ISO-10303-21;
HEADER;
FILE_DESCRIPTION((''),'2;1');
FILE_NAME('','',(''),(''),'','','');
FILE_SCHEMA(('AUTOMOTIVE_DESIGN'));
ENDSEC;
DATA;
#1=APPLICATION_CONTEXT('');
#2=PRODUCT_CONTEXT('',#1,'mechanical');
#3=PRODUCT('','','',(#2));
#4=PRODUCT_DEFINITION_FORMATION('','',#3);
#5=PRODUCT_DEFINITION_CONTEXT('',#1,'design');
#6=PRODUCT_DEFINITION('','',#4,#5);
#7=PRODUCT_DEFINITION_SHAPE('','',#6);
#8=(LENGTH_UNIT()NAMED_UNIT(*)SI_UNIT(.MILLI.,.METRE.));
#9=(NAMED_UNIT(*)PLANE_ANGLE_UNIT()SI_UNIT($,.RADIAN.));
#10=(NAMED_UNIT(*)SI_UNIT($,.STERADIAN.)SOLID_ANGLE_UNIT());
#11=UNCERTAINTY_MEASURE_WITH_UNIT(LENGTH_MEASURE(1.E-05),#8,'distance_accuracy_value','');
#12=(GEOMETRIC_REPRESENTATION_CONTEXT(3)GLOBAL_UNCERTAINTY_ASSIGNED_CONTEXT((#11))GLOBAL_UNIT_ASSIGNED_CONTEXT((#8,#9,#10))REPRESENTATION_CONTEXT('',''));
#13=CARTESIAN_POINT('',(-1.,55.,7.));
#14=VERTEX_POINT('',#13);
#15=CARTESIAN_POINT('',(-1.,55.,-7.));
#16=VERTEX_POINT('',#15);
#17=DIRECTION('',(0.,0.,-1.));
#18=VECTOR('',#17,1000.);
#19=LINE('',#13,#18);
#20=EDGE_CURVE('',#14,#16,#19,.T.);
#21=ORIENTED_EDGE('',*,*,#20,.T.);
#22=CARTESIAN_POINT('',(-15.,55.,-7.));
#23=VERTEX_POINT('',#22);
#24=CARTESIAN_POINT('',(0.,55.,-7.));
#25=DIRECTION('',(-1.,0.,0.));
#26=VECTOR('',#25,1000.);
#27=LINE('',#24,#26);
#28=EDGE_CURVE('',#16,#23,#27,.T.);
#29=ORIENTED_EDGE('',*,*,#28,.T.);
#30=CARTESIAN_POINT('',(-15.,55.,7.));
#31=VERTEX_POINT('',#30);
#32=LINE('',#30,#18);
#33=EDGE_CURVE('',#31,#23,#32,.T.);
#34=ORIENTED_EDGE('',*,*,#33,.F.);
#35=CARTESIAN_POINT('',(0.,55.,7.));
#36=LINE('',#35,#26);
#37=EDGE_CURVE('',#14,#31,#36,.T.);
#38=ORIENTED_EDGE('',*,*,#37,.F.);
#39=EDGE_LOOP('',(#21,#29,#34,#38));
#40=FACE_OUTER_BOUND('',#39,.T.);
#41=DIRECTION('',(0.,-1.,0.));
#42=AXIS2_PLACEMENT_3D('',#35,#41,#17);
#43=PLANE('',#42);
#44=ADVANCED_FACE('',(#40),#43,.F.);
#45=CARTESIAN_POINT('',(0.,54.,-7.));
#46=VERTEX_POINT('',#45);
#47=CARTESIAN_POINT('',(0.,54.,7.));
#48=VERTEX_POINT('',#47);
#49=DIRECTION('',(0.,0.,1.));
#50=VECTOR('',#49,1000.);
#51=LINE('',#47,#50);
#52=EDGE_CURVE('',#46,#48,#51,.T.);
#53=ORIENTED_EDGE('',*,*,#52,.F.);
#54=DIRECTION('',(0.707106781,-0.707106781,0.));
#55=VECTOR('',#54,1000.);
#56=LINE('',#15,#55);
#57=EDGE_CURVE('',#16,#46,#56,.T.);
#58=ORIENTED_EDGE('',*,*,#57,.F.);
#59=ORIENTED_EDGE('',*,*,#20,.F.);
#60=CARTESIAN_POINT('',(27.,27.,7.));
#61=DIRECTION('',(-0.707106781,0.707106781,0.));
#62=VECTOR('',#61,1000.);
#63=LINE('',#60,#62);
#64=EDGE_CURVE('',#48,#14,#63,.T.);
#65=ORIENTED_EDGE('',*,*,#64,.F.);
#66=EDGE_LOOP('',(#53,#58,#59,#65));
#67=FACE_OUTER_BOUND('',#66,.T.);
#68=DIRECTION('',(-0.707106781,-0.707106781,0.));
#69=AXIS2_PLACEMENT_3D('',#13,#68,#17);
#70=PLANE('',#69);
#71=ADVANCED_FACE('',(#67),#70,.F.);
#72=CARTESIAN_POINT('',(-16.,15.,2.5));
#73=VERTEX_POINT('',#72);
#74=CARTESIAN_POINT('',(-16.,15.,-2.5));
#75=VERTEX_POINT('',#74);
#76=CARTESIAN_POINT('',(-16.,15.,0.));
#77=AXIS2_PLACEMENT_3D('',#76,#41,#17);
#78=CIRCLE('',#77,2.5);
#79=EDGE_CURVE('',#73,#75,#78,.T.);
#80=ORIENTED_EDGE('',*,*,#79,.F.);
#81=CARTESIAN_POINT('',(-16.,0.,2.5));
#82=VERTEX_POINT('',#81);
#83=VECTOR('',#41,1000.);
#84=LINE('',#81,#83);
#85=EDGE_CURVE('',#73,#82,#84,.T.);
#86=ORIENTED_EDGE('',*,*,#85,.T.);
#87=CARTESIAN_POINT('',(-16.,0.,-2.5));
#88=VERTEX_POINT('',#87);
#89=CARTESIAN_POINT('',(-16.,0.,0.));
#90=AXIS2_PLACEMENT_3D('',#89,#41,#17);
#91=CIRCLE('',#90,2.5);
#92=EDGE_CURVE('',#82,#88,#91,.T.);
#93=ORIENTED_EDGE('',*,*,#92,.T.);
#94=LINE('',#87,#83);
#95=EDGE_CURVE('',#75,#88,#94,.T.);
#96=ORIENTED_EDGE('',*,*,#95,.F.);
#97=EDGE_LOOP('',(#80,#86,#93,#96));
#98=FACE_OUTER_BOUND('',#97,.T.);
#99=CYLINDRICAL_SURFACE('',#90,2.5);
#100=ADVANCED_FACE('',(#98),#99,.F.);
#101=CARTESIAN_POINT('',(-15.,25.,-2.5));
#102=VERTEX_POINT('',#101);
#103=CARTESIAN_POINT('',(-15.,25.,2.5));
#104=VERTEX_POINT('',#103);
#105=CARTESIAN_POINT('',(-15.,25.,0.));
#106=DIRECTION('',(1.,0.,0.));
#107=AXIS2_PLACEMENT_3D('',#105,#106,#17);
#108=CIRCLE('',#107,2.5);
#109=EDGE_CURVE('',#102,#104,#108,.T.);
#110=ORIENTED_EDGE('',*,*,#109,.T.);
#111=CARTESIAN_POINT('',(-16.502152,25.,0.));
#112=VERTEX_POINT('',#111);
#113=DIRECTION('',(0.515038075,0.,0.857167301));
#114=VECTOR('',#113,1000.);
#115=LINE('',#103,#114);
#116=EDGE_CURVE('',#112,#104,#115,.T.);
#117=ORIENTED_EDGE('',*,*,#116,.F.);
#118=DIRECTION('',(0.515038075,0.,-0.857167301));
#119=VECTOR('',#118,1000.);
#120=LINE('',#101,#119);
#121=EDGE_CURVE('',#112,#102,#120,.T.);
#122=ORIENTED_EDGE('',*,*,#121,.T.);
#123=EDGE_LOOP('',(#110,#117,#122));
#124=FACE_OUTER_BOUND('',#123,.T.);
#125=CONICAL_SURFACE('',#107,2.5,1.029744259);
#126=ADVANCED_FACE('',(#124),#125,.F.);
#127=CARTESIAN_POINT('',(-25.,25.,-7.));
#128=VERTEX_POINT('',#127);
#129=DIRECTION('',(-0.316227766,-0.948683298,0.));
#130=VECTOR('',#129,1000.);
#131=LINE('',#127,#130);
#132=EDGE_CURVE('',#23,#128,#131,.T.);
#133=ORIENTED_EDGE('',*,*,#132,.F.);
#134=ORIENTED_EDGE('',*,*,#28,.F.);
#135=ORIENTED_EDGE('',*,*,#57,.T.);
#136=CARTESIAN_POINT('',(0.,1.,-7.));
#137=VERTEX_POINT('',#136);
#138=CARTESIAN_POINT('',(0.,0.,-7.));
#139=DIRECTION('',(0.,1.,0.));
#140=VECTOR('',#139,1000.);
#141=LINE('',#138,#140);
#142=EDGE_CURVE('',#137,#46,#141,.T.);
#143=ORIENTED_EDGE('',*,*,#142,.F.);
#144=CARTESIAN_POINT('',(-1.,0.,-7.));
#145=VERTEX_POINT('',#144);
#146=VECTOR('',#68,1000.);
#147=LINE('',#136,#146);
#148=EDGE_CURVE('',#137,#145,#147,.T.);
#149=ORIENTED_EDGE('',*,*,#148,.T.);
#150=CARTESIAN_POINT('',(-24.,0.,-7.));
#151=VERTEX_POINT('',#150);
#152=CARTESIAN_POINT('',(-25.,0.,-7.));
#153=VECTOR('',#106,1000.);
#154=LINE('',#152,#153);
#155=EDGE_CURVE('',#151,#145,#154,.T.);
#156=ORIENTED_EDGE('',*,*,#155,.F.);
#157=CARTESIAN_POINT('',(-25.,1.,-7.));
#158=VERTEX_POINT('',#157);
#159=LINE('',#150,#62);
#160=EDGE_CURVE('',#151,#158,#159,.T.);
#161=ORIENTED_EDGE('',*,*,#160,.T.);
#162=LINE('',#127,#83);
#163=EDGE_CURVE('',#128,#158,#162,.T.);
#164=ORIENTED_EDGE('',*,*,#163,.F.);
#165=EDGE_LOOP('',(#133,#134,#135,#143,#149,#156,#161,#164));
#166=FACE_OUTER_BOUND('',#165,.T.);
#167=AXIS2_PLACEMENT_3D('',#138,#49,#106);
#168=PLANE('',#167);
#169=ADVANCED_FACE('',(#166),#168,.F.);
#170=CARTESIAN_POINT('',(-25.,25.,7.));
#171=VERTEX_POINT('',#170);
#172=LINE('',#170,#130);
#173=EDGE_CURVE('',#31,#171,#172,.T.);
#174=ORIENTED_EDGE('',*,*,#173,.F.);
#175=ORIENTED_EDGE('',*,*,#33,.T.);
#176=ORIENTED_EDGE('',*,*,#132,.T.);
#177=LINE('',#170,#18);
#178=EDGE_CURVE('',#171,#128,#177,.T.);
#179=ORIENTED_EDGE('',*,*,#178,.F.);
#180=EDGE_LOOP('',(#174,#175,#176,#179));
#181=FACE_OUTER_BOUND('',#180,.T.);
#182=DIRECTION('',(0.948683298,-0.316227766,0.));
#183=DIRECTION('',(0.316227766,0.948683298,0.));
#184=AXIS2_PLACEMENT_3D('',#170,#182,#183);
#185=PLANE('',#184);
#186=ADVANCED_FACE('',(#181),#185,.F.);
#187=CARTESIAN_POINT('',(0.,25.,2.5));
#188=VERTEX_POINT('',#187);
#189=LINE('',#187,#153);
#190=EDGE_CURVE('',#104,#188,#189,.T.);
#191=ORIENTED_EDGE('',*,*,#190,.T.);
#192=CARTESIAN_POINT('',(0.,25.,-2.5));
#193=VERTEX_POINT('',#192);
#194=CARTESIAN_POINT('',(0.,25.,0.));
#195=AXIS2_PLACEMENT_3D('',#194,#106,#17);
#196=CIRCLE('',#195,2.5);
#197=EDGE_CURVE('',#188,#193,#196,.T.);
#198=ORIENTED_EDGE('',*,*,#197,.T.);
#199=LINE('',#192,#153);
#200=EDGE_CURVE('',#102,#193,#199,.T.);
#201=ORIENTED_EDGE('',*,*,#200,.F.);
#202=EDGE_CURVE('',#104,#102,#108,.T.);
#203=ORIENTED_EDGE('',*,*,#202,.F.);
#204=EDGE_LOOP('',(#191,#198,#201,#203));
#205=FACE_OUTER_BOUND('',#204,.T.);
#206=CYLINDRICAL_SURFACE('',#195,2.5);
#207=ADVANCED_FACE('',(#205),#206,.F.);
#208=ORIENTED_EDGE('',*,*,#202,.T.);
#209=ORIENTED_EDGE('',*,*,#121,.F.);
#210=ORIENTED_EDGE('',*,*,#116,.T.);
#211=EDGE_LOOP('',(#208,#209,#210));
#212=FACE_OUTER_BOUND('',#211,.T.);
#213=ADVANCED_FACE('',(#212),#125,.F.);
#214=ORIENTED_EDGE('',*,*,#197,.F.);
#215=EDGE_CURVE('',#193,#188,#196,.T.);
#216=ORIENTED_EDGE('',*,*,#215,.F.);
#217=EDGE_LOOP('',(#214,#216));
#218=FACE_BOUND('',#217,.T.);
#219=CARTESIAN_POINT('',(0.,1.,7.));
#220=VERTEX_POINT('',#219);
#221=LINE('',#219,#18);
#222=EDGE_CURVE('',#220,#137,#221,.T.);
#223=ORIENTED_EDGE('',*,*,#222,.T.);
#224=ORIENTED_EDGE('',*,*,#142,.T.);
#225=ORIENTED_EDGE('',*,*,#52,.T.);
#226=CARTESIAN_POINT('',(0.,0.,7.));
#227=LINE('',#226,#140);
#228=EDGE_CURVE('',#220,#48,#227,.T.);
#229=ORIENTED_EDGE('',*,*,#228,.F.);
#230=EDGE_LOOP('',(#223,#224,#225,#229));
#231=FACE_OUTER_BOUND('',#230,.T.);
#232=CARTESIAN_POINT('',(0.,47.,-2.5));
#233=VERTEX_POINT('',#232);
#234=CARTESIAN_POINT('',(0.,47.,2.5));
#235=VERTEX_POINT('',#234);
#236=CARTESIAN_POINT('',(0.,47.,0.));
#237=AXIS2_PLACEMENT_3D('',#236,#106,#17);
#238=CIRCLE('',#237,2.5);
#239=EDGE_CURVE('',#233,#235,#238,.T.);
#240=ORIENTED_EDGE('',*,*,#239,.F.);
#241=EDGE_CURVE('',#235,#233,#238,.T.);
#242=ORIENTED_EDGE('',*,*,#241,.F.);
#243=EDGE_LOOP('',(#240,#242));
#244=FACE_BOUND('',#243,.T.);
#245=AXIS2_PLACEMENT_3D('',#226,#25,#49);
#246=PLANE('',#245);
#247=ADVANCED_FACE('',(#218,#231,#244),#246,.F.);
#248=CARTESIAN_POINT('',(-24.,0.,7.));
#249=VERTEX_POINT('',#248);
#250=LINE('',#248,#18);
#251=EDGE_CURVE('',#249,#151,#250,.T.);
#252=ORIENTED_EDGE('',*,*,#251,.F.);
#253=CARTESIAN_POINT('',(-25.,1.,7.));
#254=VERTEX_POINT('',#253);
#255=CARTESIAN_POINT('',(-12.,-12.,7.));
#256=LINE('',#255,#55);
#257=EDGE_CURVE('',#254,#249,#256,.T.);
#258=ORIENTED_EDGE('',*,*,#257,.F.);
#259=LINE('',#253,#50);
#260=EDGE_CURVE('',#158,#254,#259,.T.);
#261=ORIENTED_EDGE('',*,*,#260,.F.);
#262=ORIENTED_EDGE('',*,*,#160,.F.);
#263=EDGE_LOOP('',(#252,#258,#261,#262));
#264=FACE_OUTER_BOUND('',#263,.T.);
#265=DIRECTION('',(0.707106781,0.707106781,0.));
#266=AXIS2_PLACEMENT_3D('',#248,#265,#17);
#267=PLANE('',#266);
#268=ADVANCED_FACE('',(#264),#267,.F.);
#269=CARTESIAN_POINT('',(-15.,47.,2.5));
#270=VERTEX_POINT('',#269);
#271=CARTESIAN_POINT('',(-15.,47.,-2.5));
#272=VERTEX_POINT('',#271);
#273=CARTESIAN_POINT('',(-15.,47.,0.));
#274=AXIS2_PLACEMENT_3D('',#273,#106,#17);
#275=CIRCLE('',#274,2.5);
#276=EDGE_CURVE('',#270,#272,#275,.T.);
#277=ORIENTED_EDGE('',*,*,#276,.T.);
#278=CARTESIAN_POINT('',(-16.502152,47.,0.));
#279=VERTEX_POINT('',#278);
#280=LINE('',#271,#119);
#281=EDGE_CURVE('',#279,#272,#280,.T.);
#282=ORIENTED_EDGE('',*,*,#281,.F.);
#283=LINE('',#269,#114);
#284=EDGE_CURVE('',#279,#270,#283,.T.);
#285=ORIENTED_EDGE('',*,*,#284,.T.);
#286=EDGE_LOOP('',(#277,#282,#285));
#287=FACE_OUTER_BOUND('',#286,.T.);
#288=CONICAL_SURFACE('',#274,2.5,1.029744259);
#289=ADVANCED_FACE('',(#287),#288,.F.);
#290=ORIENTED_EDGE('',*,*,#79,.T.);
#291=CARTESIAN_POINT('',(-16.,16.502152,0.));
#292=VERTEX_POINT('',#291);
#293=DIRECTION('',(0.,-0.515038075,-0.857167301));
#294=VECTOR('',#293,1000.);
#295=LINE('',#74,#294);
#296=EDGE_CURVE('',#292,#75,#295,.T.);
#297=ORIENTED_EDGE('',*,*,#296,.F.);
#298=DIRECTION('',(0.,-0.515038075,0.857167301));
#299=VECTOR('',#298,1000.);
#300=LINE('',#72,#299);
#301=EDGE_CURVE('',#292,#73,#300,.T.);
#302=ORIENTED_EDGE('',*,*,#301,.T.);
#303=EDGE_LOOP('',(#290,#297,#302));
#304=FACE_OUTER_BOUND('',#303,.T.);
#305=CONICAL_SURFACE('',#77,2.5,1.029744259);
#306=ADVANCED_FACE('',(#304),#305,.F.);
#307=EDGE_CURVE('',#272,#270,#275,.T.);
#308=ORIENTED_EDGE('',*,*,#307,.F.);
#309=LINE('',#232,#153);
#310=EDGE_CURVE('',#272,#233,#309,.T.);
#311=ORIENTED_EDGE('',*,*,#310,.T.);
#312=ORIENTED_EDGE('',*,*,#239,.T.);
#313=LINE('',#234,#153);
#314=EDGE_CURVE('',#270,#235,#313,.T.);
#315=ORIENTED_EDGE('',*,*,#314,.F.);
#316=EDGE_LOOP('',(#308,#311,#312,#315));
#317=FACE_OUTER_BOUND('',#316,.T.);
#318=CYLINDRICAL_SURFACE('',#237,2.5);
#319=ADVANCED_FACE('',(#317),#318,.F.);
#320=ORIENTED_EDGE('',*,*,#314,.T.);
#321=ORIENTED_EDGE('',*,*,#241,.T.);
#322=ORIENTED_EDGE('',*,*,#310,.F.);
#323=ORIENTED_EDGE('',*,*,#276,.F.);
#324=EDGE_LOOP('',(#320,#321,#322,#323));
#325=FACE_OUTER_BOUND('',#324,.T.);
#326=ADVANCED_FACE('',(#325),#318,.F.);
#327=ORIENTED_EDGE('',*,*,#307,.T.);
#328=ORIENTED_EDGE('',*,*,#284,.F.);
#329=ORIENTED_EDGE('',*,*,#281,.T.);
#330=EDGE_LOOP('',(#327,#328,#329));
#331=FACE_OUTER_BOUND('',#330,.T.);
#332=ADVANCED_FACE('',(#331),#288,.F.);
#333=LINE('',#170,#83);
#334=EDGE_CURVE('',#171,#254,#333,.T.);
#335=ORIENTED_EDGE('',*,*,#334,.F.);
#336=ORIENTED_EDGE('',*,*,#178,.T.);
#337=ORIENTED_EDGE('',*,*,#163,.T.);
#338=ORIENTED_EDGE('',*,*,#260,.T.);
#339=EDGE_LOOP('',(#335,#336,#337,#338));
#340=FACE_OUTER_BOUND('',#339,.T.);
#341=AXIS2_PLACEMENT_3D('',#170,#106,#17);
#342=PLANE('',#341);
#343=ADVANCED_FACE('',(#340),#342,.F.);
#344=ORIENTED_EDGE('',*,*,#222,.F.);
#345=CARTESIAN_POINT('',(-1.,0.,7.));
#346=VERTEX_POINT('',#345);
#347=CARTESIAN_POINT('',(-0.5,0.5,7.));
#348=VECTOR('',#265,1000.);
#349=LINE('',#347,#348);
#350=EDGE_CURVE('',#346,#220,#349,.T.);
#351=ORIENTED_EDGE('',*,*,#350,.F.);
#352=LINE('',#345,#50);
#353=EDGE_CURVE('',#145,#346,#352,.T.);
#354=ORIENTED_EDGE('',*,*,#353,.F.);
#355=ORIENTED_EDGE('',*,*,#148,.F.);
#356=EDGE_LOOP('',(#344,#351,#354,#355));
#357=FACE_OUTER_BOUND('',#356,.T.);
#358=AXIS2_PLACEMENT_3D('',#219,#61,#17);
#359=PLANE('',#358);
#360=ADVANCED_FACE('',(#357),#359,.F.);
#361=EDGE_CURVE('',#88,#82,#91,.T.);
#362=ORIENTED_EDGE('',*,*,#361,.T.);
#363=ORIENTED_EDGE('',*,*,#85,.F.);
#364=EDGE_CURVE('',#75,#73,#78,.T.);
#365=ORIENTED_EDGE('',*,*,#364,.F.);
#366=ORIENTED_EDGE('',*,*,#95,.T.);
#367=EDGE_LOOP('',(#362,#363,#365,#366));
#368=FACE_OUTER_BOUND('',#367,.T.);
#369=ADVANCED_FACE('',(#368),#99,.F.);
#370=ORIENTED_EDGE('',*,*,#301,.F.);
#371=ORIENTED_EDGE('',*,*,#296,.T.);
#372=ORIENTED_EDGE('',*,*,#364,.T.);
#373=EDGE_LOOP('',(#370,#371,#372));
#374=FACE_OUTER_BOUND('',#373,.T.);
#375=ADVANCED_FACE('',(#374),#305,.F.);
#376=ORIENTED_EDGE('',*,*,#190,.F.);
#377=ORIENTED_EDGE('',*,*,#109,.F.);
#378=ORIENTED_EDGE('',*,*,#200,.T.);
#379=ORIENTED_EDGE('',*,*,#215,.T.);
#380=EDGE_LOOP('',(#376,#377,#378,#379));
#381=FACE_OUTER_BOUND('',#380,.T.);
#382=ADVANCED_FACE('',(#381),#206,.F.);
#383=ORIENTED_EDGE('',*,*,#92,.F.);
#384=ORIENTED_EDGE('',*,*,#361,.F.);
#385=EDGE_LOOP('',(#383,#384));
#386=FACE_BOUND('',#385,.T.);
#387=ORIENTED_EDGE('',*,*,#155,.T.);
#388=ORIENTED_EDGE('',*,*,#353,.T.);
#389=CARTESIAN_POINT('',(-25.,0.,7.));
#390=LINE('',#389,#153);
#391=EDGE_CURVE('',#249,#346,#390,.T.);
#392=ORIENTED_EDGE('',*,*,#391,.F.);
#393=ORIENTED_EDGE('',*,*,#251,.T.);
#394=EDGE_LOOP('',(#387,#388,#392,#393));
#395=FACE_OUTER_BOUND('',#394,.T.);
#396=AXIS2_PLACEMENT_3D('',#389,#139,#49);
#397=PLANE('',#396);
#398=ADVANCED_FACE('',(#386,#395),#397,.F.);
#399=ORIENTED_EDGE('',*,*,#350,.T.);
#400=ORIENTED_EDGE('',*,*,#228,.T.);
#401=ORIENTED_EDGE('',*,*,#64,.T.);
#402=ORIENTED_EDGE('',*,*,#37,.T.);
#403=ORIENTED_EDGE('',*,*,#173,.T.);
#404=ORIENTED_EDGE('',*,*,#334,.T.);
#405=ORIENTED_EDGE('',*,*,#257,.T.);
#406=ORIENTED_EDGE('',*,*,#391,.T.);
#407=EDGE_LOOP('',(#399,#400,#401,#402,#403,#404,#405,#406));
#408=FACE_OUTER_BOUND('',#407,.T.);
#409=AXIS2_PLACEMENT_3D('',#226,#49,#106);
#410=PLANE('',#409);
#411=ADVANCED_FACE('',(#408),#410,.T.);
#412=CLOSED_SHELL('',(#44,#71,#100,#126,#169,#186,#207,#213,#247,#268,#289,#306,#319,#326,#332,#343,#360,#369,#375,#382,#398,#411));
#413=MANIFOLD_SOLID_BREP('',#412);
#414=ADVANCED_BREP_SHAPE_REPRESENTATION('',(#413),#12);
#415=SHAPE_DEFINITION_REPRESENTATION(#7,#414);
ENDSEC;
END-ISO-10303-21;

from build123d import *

# Parameters (mm, degrees)
BOSS_EXTRUDE2_DEPTH   = 7
M6_TAPPED_HOLE1_D     = 5
M6_TAPPED_HOLE1_DEPTH = 15
M6_TAPPED_HOLE1_TIP   = 1.502151548
M6_TAPPED_HOLE2_D     = 5
M6_TAPPED_HOLE2_DEPTH = 15
M6_TAPPED_HOLE2_TIP   = 1.502151548
CHAMFER1_SIZE         = 1


with BuildPart() as part:
    # Sketch6 → Boss-Extrude2 (new, symmetric)
    with BuildSketch(Plane.XY):
        Polygon((0, 0), (0, 55), (-15, 55), (-25, 25), (-25, 0), align=None)
    extrude(amount=BOSS_EXTRUDE2_DEPTH, both=True)

    # M6 Tapped Hole1
    with Locations(Plane(origin=(0, 0, 0), x_dir=(0, 0, -1), z_dir=(1, 0, 0))):
        with Locations((0, 25), (0, 47)):
            Hole(M6_TAPPED_HOLE1_D / 2, depth=M6_TAPPED_HOLE1_DEPTH)
            with Locations((0, 0, -(M6_TAPPED_HOLE1_DEPTH + M6_TAPPED_HOLE1_TIP / 2))):  # 118° drill point
                Cone(0, M6_TAPPED_HOLE1_D / 2, M6_TAPPED_HOLE1_TIP, mode=Mode.SUBTRACT)

    # M6 Tapped Hole2
    with Locations(Plane(origin=(0, 0, 0), x_dir=(-1, 0, 0), z_dir=(0, -1, 0))):
        with Locations((16, 0)):
            Hole(M6_TAPPED_HOLE2_D / 2, depth=M6_TAPPED_HOLE2_DEPTH)
            with Locations((0, 0, -(M6_TAPPED_HOLE2_DEPTH + M6_TAPPED_HOLE2_TIP / 2))):  # 118° drill point
                Cone(0, M6_TAPPED_HOLE2_D / 2, M6_TAPPED_HOLE2_TIP, mode=Mode.SUBTRACT)

    # Chamfer1
    chamfer1_edges = [part.edges().sort_by_distance(p)[0] for p in [
        (-25, 0, 0),
        (0, 55, 0),
        (0, 0, 0),
    ]]
    chamfer(chamfer1_edges, length=CHAMFER1_SIZE)


solid = part.part
